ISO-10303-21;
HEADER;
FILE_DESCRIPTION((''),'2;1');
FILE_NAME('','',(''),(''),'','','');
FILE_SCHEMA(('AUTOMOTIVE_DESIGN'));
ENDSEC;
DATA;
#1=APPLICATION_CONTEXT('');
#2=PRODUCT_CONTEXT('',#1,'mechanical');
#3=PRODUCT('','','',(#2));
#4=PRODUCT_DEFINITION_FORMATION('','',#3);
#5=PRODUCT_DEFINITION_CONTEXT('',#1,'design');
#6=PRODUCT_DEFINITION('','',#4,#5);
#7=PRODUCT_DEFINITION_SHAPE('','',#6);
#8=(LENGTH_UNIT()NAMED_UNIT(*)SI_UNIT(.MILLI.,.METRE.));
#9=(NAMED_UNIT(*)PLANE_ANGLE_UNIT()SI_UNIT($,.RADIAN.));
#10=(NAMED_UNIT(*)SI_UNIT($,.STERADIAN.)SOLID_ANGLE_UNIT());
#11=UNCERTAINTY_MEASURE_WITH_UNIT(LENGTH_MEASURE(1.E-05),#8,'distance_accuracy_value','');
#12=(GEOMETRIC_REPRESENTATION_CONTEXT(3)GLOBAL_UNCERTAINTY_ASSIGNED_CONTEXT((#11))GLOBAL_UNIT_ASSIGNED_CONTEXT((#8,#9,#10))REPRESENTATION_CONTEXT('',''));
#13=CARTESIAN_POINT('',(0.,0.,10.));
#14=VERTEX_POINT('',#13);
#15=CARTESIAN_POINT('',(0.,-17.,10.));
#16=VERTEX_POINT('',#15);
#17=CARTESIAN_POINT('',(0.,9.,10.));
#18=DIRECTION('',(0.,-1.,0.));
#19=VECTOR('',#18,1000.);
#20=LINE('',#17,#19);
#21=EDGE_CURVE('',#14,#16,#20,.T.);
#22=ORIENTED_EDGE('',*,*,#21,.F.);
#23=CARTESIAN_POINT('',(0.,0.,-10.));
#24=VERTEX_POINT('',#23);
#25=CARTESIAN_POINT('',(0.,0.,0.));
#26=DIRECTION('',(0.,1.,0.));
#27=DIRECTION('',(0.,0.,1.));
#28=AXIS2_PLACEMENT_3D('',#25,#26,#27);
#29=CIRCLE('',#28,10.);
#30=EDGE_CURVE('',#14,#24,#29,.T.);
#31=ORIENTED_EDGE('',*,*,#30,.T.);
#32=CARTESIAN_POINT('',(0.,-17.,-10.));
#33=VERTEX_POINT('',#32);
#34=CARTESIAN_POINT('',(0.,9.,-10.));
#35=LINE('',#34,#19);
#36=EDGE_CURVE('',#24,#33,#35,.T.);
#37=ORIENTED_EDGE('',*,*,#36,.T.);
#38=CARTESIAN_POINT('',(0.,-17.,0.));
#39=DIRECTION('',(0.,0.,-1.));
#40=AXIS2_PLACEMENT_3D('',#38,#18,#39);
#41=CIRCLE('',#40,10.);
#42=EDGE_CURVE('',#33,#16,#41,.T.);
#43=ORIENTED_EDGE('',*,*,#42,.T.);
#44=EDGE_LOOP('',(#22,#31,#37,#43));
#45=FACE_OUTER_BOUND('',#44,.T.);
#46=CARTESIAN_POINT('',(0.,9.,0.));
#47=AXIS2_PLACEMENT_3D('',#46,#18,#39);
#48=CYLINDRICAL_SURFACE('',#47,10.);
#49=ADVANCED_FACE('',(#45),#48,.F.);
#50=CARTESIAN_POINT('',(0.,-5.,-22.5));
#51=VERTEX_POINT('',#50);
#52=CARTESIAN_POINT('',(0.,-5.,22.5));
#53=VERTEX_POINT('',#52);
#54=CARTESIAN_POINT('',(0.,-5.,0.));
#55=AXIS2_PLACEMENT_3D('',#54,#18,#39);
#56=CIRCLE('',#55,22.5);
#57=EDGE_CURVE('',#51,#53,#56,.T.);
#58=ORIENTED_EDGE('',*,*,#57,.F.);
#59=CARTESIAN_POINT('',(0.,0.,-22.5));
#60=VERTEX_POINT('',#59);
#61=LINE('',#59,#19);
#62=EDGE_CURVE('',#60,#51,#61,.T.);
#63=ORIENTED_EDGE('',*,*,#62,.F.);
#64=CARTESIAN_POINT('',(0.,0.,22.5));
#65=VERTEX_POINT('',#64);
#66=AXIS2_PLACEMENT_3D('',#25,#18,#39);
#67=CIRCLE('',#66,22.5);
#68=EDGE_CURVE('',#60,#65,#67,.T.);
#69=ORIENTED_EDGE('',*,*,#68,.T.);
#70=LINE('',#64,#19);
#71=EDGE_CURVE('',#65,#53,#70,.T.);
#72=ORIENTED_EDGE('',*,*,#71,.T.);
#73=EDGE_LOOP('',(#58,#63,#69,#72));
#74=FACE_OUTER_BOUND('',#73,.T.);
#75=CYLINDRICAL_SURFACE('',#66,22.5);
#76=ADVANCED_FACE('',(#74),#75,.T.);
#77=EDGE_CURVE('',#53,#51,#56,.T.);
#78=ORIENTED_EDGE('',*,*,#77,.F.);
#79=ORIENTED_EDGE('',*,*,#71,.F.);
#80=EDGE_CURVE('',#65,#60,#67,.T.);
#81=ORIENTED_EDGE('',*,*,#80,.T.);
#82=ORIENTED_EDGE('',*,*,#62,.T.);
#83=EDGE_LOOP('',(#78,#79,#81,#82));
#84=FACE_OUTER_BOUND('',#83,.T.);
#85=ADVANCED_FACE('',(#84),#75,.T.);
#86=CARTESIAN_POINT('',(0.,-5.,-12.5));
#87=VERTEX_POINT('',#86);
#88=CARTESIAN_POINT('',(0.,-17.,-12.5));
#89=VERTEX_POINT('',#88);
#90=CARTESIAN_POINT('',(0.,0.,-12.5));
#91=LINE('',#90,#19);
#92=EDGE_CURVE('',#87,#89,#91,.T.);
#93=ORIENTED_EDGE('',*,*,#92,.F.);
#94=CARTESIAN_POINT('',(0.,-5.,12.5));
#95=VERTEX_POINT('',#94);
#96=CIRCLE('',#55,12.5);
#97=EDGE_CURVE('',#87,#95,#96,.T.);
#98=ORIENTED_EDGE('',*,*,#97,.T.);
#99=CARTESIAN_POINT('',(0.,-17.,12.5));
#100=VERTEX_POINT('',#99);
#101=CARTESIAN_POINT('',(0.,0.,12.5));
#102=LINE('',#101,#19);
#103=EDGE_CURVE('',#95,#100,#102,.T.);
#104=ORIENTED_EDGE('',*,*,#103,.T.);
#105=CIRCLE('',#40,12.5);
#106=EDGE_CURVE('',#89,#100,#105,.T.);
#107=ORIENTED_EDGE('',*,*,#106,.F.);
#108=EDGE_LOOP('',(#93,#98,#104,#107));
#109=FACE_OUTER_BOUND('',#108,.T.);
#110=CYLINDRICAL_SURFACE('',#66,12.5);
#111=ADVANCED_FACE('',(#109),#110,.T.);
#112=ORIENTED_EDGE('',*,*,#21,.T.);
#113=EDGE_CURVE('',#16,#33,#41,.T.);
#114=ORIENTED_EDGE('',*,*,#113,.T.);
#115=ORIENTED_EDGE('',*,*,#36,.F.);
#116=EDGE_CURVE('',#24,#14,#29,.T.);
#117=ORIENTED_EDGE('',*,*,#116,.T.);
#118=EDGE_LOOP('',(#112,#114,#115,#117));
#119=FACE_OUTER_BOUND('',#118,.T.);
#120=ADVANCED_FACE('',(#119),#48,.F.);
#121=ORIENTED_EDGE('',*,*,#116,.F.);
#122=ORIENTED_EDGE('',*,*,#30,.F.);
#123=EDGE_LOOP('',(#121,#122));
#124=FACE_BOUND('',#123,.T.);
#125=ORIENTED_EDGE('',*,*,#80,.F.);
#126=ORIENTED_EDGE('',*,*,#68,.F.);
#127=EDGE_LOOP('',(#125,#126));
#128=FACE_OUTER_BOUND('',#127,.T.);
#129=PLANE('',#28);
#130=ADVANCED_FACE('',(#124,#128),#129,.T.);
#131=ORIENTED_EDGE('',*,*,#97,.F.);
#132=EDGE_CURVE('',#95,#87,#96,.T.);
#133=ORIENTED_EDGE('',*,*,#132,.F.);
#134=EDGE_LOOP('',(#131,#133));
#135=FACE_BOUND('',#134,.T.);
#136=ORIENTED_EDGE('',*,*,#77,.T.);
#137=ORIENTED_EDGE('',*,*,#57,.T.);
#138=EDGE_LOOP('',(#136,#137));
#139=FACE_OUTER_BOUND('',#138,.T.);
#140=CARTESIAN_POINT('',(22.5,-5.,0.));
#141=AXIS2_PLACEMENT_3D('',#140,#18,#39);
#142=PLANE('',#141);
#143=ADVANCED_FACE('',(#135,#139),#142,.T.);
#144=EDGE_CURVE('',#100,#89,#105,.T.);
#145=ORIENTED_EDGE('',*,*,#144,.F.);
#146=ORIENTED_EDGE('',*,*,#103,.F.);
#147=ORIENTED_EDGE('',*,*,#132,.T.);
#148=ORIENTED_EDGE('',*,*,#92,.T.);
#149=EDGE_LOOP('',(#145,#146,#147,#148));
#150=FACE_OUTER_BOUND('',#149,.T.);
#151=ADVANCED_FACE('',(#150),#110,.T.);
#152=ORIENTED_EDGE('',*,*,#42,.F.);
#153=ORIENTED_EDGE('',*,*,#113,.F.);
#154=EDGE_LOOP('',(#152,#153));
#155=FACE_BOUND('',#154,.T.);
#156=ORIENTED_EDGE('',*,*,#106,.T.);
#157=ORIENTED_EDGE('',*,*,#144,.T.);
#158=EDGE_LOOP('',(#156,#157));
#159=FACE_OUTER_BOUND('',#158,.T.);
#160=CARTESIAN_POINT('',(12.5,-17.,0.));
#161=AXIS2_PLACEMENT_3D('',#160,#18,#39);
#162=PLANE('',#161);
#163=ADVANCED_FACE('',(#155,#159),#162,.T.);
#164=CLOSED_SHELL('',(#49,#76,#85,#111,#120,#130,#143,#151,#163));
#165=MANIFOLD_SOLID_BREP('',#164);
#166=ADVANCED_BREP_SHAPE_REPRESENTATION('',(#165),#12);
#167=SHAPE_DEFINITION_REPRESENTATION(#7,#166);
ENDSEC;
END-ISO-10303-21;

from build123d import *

# Parameters (mm, degrees)
SKETCH_2_R          = 10
CUT_EXTRUDE_1_DEPTH = 26


with BuildPart() as part:
    # 草图1 → 旋转1 (revolve)
    with BuildSketch(Plane.XY, mode=Mode.PRIVATE) as revolve_1_sk:
        Polygon((0, 0), (22.5, 0), (22.5, -5), (12.5, -5), (12.5, -17), (0, -17), align=None)
    revolve(revolve_1_sk.sketch.rotate(Axis((0, 0, 0), (0, 1, 0)), 90), axis=Axis((0, 0, 0), (0, 1, 0)))

    # 草图2 → 切除-拉伸1 (cut)
    with BuildSketch(Plane.XZ.offset(17)):
        with Locations(Location((0, 0, 0), (0, 0, 270))):
            Circle(SKETCH_2_R)
    extrude(amount=-CUT_EXTRUDE_1_DEPTH, mode=Mode.SUBTRACT)


solid = part.part
